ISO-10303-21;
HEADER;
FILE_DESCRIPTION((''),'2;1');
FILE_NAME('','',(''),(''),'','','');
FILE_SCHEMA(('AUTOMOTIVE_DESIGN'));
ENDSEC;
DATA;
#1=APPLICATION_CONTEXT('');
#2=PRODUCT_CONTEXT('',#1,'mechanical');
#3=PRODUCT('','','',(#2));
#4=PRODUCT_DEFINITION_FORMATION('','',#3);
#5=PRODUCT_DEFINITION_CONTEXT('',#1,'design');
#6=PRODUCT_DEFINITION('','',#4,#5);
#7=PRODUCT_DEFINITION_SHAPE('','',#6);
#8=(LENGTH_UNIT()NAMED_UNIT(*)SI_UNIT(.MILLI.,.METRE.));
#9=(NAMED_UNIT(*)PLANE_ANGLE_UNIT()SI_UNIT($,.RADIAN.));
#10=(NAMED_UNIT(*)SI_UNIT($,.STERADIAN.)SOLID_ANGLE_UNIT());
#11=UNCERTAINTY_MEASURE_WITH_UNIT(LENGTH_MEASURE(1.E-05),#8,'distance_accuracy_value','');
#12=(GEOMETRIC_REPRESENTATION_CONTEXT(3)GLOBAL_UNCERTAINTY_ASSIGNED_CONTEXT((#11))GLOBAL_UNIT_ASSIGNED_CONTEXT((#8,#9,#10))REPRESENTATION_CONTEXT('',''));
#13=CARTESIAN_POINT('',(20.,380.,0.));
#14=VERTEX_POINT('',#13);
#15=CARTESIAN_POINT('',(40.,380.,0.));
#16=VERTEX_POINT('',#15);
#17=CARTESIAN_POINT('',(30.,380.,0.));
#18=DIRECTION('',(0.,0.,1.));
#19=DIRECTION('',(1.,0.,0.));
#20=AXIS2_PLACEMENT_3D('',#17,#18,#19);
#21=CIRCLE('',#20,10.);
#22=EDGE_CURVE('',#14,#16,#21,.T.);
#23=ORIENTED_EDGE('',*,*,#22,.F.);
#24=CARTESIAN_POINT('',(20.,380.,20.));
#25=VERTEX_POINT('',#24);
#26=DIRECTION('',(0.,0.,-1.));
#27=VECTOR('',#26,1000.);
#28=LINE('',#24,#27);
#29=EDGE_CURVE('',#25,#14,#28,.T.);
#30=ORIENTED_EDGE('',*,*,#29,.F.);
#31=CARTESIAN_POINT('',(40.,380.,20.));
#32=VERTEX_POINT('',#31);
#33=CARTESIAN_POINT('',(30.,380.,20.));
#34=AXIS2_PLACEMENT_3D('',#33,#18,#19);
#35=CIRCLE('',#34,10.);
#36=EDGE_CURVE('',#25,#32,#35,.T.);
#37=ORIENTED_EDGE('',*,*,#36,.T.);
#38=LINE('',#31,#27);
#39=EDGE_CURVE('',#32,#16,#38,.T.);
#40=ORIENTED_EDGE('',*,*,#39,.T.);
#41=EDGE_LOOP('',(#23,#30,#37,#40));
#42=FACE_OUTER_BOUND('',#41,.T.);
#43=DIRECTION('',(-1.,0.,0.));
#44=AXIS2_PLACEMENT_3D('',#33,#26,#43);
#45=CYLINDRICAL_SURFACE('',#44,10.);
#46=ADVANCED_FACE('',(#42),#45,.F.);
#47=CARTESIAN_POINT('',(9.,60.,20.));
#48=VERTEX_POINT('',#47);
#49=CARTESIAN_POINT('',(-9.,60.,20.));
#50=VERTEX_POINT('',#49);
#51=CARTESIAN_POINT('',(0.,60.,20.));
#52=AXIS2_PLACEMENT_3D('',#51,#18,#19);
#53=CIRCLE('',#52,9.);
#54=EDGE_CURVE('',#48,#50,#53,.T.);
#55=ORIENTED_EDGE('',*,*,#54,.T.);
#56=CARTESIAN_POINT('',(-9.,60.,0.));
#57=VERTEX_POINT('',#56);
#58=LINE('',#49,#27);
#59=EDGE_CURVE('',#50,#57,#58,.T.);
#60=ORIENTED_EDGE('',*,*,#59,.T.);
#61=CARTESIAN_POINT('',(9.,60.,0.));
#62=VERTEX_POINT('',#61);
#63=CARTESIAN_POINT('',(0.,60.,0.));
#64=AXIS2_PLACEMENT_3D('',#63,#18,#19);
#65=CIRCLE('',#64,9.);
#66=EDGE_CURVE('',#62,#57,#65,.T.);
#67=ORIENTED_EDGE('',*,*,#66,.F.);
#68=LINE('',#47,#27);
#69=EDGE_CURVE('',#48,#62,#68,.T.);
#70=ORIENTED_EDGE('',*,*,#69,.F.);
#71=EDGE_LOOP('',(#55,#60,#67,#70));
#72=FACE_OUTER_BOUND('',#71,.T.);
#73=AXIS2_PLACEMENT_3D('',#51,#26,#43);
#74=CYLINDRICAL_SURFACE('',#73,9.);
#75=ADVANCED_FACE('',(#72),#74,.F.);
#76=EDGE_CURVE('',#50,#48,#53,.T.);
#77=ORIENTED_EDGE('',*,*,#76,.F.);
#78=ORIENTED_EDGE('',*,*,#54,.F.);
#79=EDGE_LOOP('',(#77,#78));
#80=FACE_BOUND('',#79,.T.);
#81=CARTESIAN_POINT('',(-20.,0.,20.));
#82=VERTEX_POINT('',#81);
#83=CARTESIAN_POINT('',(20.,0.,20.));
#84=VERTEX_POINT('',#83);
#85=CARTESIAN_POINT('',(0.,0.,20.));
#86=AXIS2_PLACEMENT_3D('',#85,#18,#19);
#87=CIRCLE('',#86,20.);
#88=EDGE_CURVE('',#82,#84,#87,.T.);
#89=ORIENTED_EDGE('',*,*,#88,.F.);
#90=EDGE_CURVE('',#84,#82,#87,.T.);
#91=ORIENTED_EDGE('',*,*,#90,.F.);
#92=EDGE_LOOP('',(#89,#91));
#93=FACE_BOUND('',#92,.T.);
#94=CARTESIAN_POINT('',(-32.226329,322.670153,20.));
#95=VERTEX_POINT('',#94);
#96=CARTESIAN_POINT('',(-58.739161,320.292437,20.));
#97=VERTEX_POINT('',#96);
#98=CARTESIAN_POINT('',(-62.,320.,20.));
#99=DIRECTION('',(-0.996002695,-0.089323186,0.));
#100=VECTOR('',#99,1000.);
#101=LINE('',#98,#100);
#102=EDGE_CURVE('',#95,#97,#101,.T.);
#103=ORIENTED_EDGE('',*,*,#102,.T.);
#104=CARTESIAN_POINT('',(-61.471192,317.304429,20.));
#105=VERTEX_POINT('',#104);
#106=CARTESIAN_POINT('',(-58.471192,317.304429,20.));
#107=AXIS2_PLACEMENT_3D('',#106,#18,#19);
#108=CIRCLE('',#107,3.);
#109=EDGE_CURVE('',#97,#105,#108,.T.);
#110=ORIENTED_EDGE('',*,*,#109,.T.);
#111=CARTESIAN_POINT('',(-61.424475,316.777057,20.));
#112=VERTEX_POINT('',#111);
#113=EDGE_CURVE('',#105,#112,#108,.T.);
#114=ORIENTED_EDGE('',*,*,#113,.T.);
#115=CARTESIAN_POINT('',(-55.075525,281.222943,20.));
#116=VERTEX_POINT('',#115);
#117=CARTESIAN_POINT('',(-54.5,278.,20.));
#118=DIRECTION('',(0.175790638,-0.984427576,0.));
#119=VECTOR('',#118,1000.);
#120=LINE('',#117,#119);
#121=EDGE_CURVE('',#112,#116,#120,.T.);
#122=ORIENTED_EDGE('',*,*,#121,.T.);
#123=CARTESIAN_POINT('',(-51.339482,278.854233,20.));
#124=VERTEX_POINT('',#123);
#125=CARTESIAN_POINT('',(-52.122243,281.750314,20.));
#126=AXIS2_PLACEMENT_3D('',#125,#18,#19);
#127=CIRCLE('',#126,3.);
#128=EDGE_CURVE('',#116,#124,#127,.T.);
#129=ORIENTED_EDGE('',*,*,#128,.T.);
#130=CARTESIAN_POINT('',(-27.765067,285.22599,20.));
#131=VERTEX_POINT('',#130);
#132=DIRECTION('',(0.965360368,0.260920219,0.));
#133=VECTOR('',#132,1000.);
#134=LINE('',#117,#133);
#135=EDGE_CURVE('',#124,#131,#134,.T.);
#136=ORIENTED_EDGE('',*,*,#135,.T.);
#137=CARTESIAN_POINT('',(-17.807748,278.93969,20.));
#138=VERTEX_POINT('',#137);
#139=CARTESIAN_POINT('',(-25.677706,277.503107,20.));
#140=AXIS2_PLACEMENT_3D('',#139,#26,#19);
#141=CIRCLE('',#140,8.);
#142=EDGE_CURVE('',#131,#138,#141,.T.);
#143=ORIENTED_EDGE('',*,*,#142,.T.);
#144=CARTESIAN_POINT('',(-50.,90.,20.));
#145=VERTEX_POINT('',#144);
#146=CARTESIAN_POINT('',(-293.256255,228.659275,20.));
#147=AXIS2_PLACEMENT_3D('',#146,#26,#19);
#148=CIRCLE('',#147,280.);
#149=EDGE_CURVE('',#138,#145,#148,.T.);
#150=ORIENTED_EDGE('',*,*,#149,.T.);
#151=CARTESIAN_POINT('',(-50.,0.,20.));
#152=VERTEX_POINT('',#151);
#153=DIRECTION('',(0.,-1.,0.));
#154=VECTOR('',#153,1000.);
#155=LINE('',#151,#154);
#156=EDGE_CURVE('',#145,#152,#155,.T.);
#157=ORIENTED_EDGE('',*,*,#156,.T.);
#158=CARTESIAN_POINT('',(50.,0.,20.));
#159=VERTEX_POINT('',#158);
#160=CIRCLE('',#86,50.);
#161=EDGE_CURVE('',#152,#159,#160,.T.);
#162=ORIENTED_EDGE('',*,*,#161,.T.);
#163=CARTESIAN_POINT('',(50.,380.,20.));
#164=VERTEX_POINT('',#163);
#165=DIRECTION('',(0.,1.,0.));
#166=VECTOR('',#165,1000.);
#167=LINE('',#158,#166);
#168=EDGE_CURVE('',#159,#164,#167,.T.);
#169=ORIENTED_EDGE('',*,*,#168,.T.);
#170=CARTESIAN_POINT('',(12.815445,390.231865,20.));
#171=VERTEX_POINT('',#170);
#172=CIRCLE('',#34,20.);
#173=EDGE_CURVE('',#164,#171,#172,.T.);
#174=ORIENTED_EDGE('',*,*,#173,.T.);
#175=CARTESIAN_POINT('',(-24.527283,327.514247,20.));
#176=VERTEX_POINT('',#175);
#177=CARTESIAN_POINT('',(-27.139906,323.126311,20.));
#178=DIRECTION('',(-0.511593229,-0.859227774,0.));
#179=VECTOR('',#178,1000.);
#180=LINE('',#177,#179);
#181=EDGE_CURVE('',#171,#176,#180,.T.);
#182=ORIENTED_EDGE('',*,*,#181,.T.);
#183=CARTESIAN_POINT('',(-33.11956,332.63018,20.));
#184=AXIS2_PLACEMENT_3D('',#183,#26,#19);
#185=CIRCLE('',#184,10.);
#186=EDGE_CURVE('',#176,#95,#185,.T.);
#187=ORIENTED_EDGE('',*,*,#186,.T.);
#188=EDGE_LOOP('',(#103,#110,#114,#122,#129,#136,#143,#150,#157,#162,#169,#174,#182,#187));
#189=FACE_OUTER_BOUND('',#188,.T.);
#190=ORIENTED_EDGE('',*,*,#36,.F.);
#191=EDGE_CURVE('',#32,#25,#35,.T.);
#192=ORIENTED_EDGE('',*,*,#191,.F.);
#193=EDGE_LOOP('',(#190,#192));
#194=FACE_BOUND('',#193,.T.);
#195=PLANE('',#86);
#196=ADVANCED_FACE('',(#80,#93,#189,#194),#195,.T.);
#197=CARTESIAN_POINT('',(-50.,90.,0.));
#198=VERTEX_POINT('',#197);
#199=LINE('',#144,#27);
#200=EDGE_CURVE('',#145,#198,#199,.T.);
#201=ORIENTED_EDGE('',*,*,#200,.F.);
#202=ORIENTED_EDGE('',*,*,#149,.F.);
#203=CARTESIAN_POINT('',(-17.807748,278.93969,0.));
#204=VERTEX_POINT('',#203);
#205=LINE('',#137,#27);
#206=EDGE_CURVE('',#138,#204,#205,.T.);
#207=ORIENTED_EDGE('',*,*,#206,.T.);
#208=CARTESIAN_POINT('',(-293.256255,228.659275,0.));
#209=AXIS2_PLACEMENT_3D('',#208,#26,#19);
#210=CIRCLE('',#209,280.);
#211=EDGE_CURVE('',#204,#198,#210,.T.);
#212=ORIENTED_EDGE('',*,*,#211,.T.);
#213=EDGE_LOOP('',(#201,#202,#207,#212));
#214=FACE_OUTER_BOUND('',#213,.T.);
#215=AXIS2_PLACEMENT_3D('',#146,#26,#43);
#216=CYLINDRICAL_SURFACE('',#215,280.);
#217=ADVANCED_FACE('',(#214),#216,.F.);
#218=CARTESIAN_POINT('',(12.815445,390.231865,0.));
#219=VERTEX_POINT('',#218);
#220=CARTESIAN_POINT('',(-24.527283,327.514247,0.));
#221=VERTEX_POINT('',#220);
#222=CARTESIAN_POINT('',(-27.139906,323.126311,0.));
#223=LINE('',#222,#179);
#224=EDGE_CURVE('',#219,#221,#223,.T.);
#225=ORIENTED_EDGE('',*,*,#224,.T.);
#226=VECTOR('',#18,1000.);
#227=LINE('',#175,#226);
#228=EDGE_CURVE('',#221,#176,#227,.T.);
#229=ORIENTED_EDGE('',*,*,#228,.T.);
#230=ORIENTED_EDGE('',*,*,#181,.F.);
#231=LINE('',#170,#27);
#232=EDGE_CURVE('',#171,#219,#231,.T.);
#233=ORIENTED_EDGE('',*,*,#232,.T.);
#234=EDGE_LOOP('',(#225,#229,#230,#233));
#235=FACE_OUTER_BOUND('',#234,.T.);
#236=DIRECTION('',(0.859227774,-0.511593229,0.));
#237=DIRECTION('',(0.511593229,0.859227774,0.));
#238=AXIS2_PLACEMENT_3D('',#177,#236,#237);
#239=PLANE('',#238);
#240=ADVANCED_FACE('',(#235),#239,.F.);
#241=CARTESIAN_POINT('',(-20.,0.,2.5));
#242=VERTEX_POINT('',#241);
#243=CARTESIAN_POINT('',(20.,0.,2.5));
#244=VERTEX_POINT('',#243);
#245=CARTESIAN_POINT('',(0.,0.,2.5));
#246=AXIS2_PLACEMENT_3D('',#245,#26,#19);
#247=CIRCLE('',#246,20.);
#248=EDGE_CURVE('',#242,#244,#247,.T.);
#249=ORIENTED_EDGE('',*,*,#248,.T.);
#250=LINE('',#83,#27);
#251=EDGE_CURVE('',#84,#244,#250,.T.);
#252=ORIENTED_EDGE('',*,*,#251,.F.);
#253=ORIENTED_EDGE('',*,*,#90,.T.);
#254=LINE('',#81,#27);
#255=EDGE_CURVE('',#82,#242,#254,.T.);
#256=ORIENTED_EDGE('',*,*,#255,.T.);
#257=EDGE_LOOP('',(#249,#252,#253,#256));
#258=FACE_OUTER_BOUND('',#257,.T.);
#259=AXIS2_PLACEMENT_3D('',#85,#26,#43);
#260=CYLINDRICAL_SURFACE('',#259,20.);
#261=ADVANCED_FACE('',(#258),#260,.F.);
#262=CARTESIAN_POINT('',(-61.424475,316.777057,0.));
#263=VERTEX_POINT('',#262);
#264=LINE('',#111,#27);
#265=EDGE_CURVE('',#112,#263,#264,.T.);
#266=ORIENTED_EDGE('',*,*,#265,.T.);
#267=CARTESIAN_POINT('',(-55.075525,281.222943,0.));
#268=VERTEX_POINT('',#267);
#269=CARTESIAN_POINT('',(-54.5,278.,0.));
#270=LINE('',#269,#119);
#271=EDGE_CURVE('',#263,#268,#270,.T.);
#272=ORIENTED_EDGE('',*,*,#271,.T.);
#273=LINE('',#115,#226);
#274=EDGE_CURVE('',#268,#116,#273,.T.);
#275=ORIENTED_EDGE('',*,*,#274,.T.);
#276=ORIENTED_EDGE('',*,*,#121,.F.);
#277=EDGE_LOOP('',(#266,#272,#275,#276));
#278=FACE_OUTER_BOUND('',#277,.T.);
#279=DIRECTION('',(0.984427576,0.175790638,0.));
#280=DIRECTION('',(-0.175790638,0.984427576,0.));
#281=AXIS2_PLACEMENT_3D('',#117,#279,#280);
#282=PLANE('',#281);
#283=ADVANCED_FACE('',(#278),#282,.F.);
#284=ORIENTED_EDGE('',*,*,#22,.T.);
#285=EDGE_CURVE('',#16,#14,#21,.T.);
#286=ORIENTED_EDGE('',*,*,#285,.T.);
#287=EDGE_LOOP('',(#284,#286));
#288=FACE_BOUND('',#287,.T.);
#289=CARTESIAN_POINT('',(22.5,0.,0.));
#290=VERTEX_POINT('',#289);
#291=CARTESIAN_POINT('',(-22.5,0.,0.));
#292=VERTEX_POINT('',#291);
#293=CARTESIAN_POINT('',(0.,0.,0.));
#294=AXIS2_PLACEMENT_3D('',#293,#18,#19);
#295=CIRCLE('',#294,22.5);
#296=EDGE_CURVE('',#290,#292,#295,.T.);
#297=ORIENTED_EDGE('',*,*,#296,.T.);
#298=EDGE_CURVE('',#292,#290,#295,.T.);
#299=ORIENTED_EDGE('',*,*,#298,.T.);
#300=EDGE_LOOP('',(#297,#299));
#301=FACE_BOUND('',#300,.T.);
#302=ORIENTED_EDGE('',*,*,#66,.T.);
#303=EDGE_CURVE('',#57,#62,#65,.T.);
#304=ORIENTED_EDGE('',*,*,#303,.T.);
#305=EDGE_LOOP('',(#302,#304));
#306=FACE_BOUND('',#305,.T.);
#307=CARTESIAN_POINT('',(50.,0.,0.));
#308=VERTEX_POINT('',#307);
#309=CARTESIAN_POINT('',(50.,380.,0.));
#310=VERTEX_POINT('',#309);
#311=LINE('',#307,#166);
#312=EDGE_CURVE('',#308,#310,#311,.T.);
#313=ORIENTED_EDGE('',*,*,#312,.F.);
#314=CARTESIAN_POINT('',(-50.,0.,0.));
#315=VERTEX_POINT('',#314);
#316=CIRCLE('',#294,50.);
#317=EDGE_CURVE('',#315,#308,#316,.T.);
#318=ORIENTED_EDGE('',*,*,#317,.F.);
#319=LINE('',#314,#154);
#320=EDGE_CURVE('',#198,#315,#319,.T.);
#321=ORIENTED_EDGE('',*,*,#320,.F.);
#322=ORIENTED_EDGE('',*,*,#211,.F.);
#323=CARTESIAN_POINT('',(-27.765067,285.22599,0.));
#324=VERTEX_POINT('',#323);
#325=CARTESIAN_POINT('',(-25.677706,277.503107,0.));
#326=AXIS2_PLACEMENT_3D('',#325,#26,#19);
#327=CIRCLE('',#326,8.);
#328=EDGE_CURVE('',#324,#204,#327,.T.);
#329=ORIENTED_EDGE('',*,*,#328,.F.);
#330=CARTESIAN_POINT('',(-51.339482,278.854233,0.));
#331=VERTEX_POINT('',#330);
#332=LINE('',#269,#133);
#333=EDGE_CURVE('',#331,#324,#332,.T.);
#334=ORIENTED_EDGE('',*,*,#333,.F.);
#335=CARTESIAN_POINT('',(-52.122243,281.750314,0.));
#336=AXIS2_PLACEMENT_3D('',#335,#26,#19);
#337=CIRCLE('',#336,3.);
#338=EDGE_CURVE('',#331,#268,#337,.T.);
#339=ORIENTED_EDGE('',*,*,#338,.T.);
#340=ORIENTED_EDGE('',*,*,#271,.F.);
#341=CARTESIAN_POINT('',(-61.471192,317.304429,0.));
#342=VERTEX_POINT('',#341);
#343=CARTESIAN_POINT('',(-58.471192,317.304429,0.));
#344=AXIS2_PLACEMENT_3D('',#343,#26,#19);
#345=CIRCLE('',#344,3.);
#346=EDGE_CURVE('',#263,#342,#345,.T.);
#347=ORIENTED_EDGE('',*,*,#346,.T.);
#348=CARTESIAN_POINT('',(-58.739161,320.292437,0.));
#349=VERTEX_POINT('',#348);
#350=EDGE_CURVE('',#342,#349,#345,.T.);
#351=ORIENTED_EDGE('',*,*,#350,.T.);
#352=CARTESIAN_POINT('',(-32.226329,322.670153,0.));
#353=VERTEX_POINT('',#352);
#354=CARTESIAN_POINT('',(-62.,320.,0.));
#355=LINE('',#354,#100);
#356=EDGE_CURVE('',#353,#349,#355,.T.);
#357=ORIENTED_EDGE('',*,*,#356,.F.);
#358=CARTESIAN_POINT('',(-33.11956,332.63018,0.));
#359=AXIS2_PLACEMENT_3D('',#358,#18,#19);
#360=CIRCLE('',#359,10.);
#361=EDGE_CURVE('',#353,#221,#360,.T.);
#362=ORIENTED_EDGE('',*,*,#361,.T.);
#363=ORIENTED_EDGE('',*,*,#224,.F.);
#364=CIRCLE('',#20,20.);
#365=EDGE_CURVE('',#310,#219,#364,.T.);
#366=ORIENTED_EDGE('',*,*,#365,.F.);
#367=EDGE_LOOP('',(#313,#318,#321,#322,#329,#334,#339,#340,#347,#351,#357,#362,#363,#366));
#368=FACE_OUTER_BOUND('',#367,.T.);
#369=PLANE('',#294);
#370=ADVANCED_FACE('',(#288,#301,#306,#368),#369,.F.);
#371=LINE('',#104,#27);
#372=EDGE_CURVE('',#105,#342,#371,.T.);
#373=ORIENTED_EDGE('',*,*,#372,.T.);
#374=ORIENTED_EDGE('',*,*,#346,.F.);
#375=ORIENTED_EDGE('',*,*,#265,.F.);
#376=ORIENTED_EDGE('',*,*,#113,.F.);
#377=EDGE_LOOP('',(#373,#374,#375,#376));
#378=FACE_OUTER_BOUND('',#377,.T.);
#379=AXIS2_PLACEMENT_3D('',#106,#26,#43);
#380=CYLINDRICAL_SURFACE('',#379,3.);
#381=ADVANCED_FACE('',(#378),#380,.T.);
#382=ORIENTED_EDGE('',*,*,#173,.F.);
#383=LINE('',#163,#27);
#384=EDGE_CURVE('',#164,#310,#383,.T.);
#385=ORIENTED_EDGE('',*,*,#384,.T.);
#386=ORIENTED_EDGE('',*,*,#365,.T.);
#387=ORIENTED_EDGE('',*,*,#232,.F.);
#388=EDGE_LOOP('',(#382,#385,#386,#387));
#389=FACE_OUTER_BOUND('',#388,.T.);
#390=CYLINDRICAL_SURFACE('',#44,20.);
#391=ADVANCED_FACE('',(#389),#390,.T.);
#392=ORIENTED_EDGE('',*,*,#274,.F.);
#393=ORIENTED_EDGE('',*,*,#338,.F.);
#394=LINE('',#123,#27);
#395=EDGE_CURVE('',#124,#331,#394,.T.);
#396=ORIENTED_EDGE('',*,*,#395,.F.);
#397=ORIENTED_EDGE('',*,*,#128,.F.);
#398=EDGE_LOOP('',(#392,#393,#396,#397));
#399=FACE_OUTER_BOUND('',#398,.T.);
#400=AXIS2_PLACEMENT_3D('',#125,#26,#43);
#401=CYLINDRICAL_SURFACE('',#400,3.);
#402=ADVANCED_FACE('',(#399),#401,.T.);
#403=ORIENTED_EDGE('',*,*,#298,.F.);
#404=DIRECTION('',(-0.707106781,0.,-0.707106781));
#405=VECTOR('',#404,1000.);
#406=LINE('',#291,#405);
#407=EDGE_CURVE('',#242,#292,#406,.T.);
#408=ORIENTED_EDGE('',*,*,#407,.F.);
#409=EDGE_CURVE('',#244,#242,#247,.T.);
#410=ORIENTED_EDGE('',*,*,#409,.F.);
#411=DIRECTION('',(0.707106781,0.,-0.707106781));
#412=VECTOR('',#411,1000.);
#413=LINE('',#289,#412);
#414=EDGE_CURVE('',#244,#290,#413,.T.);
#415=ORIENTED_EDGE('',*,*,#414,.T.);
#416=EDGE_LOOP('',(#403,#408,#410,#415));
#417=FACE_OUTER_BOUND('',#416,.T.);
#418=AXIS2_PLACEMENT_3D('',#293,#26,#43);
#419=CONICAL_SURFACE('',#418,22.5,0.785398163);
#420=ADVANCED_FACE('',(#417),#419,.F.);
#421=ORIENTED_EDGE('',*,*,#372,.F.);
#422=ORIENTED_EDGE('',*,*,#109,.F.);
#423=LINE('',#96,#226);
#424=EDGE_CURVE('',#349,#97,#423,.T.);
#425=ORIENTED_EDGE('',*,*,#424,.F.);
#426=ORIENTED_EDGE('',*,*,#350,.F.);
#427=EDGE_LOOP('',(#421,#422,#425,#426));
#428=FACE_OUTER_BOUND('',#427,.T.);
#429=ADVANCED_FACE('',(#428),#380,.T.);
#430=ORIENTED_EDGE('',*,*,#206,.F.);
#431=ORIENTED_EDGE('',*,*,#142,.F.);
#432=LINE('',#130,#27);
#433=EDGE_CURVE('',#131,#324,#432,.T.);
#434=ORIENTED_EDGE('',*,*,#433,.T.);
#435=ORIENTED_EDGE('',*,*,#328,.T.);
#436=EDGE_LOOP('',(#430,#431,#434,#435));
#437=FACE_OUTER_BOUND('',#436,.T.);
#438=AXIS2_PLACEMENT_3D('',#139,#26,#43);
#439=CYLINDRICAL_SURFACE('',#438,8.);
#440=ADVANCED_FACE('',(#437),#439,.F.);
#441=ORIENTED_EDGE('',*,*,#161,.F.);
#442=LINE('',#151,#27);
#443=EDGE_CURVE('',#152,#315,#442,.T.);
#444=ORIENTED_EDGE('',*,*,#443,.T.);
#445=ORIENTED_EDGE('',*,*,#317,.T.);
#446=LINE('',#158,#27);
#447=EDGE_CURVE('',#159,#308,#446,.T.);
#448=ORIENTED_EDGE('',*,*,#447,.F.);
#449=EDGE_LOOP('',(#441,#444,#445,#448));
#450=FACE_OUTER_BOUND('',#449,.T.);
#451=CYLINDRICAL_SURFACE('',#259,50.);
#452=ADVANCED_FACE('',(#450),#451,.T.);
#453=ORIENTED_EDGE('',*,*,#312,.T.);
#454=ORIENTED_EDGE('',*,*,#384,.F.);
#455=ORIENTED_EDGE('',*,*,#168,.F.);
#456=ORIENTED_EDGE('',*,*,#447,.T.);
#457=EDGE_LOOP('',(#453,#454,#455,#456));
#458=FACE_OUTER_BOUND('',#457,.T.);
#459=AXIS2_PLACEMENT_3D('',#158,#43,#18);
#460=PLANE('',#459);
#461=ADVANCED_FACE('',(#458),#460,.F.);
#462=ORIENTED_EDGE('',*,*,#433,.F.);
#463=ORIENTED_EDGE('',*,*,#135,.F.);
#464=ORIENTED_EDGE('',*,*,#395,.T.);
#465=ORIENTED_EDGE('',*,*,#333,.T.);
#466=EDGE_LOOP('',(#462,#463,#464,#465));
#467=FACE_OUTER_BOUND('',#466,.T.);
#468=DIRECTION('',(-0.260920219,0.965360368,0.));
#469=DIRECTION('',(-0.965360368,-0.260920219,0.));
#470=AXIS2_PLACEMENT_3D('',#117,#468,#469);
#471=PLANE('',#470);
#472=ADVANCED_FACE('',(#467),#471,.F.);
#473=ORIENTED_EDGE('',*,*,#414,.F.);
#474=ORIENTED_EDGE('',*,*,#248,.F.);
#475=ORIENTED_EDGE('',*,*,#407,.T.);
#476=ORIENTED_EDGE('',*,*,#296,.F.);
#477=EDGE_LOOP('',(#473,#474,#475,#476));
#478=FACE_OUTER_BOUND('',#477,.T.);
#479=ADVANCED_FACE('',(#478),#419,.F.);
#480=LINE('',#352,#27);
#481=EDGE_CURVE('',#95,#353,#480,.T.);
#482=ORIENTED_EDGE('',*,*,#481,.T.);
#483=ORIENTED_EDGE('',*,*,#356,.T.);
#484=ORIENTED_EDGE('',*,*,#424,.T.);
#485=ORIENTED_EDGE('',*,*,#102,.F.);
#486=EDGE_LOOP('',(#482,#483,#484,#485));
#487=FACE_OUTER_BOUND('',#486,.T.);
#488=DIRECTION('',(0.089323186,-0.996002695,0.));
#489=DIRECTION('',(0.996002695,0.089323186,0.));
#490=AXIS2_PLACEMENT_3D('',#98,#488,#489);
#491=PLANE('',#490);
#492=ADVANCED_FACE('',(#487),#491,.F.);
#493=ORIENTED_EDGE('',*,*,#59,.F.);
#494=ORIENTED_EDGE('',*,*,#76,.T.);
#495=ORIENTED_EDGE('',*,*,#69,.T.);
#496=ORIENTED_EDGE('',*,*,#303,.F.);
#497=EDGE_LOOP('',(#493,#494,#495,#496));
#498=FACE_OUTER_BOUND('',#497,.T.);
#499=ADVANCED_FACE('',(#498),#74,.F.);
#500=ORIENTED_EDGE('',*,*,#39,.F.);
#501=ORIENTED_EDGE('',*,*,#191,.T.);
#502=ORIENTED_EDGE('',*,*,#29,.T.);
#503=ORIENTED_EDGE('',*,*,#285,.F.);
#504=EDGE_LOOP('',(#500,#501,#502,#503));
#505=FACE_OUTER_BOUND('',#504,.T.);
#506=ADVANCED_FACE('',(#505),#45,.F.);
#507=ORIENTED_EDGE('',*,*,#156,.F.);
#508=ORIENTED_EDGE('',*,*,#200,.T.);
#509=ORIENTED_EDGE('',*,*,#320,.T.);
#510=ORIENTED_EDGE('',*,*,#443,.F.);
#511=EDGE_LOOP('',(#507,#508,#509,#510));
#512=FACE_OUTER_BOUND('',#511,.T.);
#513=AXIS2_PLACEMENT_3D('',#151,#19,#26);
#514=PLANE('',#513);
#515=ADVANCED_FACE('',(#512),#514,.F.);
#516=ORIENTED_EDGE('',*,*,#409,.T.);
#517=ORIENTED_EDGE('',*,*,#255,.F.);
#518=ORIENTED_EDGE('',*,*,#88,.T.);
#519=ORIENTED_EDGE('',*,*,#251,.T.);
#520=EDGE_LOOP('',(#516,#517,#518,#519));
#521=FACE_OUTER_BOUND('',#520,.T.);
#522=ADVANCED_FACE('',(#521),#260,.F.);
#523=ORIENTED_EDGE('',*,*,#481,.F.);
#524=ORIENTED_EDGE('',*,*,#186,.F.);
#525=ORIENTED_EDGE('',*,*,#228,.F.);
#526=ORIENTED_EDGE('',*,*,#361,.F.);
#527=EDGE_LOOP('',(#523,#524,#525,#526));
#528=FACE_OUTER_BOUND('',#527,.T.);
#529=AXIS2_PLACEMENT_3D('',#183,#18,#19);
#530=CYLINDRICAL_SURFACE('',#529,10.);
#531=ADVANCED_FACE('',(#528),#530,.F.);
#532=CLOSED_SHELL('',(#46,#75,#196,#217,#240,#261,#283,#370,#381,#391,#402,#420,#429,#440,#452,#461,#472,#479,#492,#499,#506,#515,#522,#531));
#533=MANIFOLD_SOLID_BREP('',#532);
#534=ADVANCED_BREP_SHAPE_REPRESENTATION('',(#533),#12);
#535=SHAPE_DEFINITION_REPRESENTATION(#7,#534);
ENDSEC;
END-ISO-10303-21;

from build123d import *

# Parameters (mm, degrees)
SKETCH1_R      = 9
SKETCH1_R_2    = 10
SKETCH1_R_3    = 20
EXTRUDE1_DEPTH = 20
FILLET1_R      = 3
FILLET2_R      = 10
CHAMFER1_SIZE  = 2.5


with BuildPart() as part:
    # Sketch1 → Extrude1 (new body)
    with BuildSketch(Plane.XY):
        with BuildLine():
            Line((-54.5, 278), (-62, 320))
            Line((-62, 320), (-27.139905674, 323.126311493))
            Line((-27.139905674, 323.126311493), (12.815444518, 390.231864585))
            ThreePointArc((12.815444518, 390.231864585), (35.306076251, 399.283297302), (50, 380))
            Line((50, 380), (50, 0))
            ThreePointArc((50, 0), (0, -50), (-50, 0))
            Line((-50, 0), (-50, 90))
            ThreePointArc((-50, 90), (-17.234137889, 181.62959318), (-17.807748235, 278.939690485))
            ThreePointArc((-17.807748235, 278.939690485), (-21.406992079, 284.267795368), (-27.765067315, 285.22599012))
            Line((-27.765067315, 285.22599012), (-54.5, 278))
        make_face()
        with Locations((0, 60)):
            Circle(SKETCH1_R, mode=Mode.SUBTRACT)
        with Locations((30, 380)):
            Circle(SKETCH1_R_2, mode=Mode.SUBTRACT)
        Circle(SKETCH1_R_3, mode=Mode.SUBTRACT)
    extrude(amount=EXTRUDE1_DEPTH)

    # Fillet1
    fillet1_edges = [part.edges().sort_by_distance(p)[0] for p in [
        (-54.5, 278, 10),
        (-62, 320, 10),
    ]]
    fillet(fillet1_edges, radius=FILLET1_R)

    # Fillet2
    fillet2_edges = [part.edges().sort_by_distance(p)[0] for p in [
        (-27.139905674, 323.126311493, 10),
    ]]
    fillet(fillet2_edges, radius=FILLET2_R)

    # Chamfer1
    chamfer1_edges = [part.edges().sort_by_distance(p)[0] for p in [
        (-20, 0, 0),
    ]]
    chamfer(chamfer1_edges, length=CHAMFER1_SIZE)


solid = part.part
